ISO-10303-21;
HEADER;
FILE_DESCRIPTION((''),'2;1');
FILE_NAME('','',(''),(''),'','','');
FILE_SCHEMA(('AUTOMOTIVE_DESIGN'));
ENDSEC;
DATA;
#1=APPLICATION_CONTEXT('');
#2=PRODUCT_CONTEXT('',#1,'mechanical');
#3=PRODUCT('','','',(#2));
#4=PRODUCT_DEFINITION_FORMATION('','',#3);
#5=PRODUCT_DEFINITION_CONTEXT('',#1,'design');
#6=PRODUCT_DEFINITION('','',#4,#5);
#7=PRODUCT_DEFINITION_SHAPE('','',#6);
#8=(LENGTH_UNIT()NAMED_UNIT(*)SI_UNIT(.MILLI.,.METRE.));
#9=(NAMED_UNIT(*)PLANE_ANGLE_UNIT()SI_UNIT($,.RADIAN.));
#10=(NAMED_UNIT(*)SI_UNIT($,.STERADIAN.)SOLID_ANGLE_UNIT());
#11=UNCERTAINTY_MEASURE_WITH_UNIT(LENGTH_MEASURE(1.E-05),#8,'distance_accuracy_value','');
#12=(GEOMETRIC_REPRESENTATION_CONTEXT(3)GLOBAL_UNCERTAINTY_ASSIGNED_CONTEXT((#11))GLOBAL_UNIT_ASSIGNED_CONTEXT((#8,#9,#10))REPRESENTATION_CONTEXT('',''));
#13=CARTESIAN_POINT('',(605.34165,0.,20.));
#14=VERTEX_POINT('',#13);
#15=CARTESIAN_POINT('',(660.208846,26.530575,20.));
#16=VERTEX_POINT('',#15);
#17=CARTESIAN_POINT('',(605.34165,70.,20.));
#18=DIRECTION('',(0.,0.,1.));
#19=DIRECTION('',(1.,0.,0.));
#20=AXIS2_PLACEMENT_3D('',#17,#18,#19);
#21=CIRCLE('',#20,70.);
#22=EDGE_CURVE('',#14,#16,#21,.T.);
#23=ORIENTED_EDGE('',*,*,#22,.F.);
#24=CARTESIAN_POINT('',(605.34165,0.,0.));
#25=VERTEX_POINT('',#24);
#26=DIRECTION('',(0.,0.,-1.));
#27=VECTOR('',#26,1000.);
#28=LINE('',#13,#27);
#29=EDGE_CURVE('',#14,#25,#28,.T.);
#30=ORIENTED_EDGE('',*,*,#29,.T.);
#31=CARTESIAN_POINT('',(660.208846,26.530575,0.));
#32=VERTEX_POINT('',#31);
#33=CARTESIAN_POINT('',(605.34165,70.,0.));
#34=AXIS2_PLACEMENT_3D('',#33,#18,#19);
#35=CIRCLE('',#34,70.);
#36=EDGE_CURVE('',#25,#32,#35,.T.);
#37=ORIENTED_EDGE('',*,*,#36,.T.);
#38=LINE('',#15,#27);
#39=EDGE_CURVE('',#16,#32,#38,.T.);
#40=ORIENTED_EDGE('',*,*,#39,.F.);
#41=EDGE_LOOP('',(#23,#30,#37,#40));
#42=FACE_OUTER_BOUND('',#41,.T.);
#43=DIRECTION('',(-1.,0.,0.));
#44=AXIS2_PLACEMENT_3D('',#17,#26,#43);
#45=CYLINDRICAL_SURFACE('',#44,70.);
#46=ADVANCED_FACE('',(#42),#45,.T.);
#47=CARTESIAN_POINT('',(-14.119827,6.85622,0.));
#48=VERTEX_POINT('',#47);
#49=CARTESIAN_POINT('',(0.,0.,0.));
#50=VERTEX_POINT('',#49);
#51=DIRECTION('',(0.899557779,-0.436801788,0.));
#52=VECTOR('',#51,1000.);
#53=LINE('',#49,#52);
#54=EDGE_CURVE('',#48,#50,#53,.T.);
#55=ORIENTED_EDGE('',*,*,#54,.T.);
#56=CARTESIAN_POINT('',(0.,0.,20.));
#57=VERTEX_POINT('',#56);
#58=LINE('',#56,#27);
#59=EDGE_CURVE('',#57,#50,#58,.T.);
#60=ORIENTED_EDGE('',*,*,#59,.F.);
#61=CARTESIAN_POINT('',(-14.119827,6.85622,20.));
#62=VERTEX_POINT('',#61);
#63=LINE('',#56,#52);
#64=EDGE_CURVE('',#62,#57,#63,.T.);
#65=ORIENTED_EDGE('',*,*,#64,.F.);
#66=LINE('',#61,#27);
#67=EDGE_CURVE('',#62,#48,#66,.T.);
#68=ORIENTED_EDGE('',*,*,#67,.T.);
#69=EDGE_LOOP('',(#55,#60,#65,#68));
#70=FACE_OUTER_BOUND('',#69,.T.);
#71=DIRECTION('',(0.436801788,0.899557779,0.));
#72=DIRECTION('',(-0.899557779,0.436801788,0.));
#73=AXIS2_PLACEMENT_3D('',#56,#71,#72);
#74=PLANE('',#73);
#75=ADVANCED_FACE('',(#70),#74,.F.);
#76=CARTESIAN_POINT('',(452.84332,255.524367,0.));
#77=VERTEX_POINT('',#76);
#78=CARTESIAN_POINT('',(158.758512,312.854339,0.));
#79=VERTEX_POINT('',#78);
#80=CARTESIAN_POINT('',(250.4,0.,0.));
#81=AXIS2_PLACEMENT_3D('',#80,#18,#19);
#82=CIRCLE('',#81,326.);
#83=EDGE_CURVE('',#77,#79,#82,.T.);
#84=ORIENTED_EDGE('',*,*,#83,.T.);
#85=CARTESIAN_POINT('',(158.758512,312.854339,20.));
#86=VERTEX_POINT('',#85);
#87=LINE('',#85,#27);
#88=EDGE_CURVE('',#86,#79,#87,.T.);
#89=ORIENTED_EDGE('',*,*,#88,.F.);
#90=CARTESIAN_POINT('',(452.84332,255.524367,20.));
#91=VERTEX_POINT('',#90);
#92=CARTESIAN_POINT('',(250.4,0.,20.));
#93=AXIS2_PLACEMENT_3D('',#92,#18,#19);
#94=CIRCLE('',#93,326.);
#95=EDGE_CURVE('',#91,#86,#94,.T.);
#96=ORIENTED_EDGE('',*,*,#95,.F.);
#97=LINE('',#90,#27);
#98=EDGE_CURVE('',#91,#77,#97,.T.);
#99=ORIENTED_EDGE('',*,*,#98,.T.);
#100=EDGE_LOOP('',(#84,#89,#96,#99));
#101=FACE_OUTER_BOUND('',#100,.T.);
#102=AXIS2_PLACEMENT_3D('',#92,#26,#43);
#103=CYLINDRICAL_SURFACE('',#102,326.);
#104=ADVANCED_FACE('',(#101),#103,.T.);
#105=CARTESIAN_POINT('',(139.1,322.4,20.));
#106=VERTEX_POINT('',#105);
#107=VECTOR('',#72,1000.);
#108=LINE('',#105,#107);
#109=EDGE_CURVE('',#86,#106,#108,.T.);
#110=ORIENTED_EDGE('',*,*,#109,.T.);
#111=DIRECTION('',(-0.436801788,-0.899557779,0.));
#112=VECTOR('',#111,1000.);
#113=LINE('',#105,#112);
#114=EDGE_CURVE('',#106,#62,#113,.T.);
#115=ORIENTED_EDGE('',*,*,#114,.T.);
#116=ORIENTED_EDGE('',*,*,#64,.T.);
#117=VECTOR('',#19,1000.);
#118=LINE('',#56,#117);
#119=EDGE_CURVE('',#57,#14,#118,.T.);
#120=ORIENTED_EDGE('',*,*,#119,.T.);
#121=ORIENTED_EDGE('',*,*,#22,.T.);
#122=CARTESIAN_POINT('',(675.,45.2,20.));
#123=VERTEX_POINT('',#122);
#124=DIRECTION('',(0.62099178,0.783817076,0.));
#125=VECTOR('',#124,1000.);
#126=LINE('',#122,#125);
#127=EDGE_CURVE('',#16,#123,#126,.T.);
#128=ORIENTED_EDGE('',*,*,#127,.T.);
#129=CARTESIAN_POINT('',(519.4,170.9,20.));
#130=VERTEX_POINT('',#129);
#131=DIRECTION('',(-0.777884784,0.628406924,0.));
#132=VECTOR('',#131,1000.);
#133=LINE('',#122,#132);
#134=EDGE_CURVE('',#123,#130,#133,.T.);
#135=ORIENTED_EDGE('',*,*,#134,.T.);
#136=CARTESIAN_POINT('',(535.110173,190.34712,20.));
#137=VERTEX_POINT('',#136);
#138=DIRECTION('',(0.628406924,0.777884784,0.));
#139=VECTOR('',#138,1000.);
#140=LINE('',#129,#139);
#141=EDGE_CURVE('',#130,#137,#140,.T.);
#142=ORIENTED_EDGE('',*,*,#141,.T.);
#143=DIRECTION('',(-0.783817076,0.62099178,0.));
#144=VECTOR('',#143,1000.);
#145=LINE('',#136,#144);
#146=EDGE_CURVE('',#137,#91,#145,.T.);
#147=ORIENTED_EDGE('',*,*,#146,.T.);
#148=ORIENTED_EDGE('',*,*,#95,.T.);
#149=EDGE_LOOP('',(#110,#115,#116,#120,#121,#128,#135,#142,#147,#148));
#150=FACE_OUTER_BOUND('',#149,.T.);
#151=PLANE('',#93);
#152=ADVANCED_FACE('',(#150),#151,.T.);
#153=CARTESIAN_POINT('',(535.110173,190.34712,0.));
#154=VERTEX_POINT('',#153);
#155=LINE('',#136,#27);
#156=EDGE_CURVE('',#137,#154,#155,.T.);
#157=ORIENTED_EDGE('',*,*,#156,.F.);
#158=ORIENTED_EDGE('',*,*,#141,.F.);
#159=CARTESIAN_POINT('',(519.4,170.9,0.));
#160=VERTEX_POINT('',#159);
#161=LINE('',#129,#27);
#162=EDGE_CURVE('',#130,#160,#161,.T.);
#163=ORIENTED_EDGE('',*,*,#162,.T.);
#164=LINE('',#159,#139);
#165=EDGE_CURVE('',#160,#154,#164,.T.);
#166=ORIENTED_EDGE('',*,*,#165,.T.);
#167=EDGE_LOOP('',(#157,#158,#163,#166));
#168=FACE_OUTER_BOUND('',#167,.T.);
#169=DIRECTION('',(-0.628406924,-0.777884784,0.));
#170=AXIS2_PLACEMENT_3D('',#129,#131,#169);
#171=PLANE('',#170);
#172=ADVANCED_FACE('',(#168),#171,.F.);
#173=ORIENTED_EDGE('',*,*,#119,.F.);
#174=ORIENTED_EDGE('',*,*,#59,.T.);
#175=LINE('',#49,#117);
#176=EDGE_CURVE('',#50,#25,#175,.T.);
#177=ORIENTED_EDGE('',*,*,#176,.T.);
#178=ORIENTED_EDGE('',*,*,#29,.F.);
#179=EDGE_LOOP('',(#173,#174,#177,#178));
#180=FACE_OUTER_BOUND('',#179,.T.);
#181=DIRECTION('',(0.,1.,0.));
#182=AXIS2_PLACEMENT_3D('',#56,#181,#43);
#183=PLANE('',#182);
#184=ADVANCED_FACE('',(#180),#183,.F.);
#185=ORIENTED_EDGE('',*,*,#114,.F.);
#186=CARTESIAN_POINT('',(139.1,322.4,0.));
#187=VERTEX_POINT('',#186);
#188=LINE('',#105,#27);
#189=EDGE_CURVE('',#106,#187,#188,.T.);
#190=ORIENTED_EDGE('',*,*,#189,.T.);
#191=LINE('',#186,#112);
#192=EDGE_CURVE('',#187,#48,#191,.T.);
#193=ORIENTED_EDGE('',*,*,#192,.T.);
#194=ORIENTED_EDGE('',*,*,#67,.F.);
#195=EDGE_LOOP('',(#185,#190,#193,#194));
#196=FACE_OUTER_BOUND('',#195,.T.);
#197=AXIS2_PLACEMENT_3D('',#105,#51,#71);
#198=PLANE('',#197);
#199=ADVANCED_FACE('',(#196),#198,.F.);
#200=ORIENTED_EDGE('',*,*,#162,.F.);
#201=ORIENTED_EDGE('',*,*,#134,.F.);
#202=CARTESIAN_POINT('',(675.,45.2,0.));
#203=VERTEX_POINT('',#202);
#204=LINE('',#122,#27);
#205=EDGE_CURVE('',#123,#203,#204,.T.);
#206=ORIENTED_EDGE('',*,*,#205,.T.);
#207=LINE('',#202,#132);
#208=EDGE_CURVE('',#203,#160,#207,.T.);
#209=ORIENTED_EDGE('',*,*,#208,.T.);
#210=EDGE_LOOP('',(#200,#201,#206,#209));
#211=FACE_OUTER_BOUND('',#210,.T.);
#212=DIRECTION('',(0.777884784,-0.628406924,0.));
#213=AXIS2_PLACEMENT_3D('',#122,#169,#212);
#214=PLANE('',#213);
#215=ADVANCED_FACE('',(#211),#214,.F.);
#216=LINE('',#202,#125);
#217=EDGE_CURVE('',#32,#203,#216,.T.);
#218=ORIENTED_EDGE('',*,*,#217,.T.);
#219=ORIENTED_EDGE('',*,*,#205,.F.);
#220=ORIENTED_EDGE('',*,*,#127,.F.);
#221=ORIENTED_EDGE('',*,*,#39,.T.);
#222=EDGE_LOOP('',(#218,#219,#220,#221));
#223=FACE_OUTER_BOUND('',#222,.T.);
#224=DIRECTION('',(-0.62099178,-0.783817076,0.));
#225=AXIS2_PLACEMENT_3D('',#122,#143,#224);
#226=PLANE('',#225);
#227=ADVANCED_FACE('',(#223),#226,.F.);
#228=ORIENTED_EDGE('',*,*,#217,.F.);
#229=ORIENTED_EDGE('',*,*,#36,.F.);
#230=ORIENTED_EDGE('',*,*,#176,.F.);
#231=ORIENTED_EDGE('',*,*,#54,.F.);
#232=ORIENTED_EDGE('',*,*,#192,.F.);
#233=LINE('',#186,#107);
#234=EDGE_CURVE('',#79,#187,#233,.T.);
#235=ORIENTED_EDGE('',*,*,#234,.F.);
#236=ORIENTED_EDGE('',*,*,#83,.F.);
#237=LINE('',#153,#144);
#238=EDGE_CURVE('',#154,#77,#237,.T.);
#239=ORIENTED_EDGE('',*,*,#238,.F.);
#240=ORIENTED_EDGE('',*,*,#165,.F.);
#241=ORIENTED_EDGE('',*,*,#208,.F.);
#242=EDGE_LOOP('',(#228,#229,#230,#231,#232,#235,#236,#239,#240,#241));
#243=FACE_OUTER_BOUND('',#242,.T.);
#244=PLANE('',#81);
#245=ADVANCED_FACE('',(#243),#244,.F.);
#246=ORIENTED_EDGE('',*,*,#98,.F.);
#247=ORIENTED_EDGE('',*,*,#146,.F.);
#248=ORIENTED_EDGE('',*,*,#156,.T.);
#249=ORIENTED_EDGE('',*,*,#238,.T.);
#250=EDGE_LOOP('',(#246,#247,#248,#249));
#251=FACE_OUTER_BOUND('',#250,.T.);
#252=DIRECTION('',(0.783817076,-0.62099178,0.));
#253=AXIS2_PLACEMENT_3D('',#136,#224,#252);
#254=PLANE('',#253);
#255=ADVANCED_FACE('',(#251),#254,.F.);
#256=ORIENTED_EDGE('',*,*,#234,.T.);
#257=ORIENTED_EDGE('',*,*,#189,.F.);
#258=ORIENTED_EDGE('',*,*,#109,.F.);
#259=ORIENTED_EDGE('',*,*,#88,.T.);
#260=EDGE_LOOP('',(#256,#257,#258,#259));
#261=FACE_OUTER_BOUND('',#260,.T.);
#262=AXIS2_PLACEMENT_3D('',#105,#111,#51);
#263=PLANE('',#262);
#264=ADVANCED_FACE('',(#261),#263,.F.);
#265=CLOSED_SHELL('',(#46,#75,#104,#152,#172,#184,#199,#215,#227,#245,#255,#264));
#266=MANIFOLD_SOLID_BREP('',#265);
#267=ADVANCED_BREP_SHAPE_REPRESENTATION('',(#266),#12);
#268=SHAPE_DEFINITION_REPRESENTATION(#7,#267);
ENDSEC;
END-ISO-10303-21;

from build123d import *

# Parameters (mm, degrees)
BOSS_EXTRUDE1_DEPTH = 20


with BuildPart() as part:
    # Sketch1 → Boss-Extrude1 (new body)
    with BuildSketch(Plane.XY):
        with BuildLine():
            Line((0, 0), (605.341650479, 0))
            ThreePointArc((605.341650479, 0), (635.814099319, 6.980718334), (660.208845808, 26.53057538))
            Line((660.208845808, 26.53057538), (675, 45.2))
            Line((675, 45.2), (519.4, 170.9))
            Line((519.4, 170.9), (535.110173103, 190.347119609))
            Line((535.110173103, 190.347119609), (452.843320373, 255.524366816))
            ThreePointArc((452.843320373, 255.524366816), (312.777423466, 319.976650776), (158.75851208, 312.854339417))
            Line((158.75851208, 312.854339417), (139.1, 322.4))
            Line((139.1, 322.4), (-14.119827283, 6.856219748))
            Line((-14.119827283, 6.856219748), (0, 0))
        make_face()
    extrude(amount=BOSS_EXTRUDE1_DEPTH)


solid = part.part
